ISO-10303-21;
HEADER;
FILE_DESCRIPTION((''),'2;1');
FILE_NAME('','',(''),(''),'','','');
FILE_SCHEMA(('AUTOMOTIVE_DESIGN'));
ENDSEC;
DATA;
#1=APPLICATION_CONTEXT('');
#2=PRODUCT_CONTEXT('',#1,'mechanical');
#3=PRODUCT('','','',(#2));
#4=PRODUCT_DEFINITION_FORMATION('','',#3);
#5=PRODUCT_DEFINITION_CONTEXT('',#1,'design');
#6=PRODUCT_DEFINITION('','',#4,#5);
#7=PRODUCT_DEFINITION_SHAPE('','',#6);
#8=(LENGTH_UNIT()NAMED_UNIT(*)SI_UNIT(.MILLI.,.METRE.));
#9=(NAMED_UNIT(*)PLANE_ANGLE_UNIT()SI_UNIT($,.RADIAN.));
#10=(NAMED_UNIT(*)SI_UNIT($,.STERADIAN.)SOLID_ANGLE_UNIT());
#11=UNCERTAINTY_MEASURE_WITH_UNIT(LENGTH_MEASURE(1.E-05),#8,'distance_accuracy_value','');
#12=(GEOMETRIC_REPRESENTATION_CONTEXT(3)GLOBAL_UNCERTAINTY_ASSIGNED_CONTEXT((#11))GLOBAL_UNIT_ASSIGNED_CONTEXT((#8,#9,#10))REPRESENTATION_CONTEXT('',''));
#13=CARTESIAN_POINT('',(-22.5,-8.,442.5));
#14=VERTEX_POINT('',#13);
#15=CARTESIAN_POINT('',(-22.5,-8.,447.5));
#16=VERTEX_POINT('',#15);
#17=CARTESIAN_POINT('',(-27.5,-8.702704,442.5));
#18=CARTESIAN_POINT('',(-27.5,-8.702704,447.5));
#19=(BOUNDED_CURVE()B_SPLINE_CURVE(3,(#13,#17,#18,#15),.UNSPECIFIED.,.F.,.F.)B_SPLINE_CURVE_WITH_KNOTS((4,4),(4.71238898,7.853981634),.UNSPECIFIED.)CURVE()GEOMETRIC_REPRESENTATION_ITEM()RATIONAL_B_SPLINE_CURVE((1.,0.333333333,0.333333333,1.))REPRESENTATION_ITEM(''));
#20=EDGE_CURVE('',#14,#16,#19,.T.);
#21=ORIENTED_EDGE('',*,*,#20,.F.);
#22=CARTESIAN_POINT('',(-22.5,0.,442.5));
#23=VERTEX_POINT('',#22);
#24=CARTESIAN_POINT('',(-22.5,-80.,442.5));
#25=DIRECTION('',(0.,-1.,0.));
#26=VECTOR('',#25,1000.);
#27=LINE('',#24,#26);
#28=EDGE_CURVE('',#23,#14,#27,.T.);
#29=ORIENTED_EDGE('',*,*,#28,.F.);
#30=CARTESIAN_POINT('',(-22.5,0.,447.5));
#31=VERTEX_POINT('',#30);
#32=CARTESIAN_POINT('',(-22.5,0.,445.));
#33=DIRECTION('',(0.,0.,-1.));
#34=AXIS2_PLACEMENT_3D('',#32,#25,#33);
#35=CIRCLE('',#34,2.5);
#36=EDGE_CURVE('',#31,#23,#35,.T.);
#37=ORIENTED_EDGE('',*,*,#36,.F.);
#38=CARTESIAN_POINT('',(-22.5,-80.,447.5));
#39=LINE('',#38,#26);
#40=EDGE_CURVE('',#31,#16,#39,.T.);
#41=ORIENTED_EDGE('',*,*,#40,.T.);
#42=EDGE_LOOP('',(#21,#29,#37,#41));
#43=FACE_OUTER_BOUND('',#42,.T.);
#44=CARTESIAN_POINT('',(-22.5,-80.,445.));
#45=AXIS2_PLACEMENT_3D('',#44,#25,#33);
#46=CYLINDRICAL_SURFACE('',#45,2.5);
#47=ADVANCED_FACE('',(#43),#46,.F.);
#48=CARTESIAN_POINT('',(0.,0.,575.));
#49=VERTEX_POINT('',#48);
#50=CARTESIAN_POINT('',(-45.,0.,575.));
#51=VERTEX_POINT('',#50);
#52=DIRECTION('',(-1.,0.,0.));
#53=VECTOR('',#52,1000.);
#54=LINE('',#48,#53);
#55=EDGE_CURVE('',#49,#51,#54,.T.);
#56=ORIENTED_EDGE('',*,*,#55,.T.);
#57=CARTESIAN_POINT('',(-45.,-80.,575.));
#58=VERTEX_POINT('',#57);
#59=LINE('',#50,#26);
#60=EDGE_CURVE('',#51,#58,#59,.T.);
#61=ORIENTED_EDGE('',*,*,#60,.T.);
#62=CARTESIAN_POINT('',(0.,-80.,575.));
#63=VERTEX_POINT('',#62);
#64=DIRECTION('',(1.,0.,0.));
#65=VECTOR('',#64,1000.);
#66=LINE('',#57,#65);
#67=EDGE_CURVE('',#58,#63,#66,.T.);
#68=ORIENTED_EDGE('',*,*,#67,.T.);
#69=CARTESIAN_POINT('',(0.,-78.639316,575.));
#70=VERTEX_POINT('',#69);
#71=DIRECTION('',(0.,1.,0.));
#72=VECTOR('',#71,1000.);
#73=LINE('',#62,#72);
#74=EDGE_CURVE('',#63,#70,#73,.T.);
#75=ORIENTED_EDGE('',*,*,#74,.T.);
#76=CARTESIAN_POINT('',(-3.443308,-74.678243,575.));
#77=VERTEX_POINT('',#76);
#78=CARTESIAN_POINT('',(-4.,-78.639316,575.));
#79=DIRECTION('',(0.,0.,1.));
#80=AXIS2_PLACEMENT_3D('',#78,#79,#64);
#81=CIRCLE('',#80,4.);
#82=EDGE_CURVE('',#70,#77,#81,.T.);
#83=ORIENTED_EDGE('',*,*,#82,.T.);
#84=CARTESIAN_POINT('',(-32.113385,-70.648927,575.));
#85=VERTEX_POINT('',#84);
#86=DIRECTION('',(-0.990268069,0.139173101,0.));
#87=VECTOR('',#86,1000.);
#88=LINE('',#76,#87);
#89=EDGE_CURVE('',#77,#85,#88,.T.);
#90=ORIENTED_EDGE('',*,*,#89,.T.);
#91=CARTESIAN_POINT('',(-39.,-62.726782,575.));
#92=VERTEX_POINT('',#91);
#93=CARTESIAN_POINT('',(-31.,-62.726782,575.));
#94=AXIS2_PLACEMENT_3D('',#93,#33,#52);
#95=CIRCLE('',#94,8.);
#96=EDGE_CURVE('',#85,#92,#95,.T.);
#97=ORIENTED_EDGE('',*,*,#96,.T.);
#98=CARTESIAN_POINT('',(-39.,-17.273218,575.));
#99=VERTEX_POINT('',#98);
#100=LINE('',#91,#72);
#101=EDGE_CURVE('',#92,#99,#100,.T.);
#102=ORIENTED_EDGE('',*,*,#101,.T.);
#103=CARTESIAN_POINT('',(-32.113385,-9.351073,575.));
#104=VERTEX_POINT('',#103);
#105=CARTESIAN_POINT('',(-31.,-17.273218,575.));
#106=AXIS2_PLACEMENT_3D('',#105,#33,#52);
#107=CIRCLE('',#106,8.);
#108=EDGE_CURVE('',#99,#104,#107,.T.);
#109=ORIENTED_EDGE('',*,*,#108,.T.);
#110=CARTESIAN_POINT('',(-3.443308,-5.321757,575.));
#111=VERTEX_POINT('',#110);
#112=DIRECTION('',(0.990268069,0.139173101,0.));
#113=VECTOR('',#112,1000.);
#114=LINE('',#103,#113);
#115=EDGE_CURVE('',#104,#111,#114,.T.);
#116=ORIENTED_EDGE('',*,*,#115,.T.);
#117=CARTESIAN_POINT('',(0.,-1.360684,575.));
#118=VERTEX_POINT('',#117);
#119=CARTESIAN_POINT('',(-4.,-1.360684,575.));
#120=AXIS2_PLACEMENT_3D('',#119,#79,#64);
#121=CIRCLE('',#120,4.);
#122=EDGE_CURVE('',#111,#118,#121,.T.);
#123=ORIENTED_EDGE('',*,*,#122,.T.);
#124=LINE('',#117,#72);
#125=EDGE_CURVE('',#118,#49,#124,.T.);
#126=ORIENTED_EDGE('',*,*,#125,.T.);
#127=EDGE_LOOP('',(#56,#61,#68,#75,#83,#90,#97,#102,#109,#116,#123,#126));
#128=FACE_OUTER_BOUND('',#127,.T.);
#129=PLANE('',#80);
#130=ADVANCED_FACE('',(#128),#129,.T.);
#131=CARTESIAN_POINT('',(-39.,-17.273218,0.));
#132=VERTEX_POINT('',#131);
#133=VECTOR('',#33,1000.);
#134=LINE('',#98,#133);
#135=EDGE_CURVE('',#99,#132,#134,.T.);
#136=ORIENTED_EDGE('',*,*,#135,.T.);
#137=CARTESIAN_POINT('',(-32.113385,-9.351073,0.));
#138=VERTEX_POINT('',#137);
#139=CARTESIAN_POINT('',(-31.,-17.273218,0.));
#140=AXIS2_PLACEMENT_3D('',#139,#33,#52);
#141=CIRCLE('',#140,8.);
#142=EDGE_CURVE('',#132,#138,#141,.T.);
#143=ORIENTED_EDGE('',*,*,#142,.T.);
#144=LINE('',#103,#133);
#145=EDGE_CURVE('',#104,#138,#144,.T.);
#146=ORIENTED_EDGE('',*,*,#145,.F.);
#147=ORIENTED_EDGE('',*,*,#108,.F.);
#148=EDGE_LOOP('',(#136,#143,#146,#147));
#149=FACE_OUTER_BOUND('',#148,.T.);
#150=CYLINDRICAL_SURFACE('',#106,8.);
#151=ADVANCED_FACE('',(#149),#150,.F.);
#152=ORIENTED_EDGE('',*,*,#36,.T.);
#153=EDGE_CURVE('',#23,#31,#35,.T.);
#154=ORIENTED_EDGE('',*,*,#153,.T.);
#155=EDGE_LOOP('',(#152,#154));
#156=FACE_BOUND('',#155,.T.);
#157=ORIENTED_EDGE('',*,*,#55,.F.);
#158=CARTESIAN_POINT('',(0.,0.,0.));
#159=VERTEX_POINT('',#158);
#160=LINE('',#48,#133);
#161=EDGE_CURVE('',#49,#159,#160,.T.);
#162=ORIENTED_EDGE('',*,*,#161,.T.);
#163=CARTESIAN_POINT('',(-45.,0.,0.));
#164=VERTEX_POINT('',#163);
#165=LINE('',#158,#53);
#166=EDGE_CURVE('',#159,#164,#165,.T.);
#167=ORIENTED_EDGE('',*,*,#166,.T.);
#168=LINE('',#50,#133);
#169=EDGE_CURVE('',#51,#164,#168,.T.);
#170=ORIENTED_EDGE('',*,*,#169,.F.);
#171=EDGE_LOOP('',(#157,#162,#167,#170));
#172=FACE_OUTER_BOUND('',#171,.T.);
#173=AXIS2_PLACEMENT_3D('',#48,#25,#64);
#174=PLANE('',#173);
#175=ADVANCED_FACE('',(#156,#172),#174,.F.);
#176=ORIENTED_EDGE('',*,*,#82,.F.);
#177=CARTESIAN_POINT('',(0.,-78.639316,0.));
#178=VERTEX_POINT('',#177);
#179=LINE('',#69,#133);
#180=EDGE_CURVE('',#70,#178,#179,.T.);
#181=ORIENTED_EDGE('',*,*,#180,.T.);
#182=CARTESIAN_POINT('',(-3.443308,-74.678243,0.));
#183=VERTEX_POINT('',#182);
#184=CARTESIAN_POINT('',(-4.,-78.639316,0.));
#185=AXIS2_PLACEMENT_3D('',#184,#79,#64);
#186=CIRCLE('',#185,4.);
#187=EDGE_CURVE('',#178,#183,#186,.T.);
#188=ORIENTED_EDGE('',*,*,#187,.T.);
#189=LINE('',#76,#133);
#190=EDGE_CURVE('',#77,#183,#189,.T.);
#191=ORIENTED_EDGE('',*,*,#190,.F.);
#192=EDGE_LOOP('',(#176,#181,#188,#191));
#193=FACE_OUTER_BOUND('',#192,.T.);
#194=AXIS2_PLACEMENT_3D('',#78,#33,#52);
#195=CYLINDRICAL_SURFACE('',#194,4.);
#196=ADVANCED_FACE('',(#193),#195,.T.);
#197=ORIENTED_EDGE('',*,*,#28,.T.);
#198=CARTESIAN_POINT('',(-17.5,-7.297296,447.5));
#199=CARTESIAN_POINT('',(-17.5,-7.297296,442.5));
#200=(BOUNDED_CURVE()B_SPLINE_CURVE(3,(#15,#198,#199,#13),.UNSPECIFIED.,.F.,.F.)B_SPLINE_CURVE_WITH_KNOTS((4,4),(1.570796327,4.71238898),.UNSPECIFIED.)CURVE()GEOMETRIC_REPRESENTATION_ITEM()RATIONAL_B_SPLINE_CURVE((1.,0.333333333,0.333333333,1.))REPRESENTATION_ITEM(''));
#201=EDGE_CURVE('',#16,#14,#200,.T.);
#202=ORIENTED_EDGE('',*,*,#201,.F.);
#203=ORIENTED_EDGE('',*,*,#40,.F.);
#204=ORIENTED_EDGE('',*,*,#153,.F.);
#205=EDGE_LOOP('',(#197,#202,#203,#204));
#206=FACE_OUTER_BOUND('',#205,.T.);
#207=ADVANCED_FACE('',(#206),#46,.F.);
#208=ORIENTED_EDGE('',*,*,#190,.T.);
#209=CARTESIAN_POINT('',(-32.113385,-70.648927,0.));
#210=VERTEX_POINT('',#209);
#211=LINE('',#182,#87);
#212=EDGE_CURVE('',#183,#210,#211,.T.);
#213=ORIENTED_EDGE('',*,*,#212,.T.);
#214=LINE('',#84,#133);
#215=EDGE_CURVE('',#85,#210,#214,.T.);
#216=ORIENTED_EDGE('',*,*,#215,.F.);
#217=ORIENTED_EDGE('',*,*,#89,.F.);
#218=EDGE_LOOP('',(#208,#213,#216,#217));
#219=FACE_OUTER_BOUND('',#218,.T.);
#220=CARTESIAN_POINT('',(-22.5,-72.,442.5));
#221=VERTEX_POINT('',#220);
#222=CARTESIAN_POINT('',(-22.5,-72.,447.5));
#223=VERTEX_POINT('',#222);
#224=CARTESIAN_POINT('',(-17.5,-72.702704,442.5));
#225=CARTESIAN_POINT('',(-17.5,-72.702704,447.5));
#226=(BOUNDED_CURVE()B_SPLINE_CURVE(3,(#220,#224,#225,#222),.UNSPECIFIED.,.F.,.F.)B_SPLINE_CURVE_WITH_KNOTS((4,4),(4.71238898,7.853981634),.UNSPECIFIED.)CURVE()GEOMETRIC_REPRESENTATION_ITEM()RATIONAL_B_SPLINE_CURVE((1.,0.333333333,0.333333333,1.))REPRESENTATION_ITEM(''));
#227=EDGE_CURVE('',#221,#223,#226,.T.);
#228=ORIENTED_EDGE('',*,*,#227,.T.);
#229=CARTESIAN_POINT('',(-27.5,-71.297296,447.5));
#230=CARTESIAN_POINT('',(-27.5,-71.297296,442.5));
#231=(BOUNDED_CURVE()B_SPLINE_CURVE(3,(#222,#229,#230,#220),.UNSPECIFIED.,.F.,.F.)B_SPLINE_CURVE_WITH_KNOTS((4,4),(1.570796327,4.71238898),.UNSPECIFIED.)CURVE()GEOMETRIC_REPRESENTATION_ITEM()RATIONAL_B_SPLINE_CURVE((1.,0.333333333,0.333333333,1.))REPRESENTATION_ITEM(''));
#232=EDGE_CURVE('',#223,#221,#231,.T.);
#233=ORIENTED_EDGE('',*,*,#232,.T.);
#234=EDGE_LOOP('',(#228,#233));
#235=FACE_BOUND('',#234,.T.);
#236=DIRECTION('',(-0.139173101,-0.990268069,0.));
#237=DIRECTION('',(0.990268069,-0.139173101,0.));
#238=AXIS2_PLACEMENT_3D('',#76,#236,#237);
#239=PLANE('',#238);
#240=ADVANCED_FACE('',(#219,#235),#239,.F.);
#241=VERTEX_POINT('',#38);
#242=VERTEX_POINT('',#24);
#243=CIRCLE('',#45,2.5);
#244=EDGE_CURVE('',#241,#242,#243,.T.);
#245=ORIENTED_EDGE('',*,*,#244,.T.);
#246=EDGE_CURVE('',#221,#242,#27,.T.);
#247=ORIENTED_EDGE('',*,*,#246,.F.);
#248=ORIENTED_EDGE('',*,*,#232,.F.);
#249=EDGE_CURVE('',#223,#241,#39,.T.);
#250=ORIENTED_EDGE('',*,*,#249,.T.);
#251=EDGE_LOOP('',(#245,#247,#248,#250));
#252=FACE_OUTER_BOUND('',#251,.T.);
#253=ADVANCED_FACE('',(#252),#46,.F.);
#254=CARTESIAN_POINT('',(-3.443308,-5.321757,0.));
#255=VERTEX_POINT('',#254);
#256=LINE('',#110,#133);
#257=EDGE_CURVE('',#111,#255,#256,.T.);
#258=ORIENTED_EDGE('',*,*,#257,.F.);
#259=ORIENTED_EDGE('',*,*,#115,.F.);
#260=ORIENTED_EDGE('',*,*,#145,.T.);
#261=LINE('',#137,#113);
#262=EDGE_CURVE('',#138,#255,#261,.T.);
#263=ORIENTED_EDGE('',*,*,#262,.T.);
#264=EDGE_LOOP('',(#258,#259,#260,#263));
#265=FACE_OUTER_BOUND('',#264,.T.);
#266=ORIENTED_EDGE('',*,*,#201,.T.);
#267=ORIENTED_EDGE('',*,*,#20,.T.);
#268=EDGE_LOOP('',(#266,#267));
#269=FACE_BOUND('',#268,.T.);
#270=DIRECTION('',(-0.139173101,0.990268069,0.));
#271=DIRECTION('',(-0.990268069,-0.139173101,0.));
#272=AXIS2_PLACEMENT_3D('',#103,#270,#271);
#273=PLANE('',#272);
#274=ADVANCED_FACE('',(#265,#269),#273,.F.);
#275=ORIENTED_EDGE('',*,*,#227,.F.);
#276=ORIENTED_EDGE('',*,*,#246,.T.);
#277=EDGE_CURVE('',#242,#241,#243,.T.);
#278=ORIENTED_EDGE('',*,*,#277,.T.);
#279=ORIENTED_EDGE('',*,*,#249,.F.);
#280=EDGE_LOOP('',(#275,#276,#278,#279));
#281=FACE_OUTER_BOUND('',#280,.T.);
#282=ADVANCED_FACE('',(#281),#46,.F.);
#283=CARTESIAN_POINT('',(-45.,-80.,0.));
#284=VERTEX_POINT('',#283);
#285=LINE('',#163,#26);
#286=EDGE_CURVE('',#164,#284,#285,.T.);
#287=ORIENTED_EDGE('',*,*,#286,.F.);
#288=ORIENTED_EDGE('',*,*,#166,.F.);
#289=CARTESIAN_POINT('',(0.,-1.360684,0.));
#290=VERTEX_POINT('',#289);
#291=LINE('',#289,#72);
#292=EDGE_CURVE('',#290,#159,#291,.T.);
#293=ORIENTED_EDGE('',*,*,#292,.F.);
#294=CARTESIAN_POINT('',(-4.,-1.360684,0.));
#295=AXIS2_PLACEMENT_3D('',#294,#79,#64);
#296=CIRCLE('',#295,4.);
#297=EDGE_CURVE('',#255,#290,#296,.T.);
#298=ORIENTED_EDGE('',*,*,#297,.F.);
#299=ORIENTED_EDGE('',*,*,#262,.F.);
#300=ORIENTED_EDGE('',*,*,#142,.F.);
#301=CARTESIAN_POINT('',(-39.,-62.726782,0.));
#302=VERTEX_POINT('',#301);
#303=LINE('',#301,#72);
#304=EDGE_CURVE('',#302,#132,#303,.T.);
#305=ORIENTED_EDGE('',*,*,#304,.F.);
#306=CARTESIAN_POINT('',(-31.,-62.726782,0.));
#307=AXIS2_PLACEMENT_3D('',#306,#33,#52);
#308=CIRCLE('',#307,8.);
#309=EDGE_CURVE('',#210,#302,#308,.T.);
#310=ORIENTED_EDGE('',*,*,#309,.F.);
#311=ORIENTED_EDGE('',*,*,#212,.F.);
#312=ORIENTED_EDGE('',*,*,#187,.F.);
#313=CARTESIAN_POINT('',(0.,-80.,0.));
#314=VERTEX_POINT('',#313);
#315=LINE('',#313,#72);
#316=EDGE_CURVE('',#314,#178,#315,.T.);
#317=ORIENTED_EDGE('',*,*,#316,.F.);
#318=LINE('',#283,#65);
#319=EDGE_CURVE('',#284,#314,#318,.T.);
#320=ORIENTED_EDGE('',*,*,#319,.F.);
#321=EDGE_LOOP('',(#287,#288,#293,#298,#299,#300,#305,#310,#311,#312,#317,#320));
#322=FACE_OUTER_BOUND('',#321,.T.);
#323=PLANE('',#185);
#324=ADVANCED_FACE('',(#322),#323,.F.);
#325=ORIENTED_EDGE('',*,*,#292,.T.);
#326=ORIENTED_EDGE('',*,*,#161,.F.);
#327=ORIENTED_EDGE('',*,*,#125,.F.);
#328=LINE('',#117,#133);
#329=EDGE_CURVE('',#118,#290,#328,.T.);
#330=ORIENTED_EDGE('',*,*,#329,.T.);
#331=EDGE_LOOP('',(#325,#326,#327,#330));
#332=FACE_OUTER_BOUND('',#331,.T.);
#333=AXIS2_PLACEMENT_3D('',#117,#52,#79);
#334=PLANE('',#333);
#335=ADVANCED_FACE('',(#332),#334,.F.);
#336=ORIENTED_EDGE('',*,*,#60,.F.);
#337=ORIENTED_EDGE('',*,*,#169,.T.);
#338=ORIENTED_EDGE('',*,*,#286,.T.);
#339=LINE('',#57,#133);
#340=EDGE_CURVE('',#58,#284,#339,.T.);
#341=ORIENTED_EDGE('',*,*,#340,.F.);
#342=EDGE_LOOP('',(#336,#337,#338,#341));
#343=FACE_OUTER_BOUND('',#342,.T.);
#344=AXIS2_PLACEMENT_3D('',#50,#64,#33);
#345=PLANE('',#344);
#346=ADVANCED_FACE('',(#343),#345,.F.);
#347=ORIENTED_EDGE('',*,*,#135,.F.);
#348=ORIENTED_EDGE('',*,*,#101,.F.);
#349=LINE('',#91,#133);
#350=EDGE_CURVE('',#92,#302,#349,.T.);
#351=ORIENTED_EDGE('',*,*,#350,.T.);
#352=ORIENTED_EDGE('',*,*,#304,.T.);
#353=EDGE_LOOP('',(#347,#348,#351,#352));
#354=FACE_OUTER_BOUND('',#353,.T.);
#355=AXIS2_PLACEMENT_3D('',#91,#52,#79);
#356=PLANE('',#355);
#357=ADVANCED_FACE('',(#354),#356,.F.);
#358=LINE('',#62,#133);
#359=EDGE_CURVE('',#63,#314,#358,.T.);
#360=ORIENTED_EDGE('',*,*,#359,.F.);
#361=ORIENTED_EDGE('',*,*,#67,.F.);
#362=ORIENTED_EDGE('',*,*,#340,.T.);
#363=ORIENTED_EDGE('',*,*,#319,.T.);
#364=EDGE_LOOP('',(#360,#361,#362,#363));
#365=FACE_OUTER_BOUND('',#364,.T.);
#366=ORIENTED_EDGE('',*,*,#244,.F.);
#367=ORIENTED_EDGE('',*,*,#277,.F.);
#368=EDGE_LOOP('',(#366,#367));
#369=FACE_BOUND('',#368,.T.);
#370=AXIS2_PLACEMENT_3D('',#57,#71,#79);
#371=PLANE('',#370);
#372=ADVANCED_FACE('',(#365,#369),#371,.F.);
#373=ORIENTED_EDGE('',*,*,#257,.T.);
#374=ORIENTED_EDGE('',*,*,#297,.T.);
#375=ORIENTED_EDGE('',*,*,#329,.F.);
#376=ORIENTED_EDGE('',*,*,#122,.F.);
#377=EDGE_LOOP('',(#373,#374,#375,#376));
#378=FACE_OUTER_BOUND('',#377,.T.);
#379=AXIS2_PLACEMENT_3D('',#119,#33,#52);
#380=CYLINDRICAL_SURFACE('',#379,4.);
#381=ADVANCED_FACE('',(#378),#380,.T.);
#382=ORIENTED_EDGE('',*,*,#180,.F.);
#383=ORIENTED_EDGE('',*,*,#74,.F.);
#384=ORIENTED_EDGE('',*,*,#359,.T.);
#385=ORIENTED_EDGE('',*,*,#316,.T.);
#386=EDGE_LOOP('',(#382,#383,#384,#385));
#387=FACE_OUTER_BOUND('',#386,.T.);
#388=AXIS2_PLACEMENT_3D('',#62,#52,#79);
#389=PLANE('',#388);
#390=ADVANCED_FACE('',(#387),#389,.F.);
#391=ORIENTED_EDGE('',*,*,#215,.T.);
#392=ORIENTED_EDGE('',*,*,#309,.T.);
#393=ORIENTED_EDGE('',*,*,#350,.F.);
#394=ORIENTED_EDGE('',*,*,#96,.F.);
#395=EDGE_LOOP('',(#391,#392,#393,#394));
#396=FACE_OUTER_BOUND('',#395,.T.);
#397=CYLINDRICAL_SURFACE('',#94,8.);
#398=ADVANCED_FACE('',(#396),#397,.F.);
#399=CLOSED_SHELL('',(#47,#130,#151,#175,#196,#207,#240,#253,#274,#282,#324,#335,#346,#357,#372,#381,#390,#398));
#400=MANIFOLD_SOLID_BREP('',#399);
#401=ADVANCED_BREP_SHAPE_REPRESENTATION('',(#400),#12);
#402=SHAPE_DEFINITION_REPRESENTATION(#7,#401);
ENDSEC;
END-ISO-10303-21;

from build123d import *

# Parameters (mm, degrees)
EXTRUDE_1_DEPTH    = 575
HOLE_WIZARD_M6_1_D = 5


with BuildPart() as part:
    # 草图1 → 凸台-拉伸1 (new body)
    with BuildSketch(Plane.XY):
        with BuildLine():
            Line((0, 0), (-45, 0))
            Line((-45, 0), (-45, -80))
            Line((-45, -80), (0, -80))
            Line((0, -80), (0, -78.639315732))
            ThreePointArc((0, -78.639315732), (-0.981161679, -76.015079616), (-3.443307596, -74.678243457))
            Line((-3.443307596, -74.678243457), (-32.113384808, -70.648926875))
            ThreePointArc((-32.113384808, -70.648926875), (-37.037676642, -67.975254557), (-39, -62.726782325))
            Line((-39, -62.726782325), (-39, -17.273217675))
            ThreePointArc((-39, -17.273217675), (-37.037676642, -12.024745443), (-32.113384808, -9.351073125))
            Line((-32.113384808, -9.351073125), (-3.443307596, -5.321756543))
            ThreePointArc((-3.443307596, -5.321756543), (-0.981161679, -3.984920384), (0, -1.360684268))
            Line((0, -1.360684268), (0, 0))
        make_face()
    extrude(amount=EXTRUDE_1_DEPTH)

    # M6 螺纹孔1 (through all)
    with Locations(Plane(origin=(0, -80, 0), x_dir=(-1, 0, 0), z_dir=(0, -1, 0))):
        with Locations((22.5, -445)):
            Hole(HOLE_WIZARD_M6_1_D / 2)


solid = part.part
